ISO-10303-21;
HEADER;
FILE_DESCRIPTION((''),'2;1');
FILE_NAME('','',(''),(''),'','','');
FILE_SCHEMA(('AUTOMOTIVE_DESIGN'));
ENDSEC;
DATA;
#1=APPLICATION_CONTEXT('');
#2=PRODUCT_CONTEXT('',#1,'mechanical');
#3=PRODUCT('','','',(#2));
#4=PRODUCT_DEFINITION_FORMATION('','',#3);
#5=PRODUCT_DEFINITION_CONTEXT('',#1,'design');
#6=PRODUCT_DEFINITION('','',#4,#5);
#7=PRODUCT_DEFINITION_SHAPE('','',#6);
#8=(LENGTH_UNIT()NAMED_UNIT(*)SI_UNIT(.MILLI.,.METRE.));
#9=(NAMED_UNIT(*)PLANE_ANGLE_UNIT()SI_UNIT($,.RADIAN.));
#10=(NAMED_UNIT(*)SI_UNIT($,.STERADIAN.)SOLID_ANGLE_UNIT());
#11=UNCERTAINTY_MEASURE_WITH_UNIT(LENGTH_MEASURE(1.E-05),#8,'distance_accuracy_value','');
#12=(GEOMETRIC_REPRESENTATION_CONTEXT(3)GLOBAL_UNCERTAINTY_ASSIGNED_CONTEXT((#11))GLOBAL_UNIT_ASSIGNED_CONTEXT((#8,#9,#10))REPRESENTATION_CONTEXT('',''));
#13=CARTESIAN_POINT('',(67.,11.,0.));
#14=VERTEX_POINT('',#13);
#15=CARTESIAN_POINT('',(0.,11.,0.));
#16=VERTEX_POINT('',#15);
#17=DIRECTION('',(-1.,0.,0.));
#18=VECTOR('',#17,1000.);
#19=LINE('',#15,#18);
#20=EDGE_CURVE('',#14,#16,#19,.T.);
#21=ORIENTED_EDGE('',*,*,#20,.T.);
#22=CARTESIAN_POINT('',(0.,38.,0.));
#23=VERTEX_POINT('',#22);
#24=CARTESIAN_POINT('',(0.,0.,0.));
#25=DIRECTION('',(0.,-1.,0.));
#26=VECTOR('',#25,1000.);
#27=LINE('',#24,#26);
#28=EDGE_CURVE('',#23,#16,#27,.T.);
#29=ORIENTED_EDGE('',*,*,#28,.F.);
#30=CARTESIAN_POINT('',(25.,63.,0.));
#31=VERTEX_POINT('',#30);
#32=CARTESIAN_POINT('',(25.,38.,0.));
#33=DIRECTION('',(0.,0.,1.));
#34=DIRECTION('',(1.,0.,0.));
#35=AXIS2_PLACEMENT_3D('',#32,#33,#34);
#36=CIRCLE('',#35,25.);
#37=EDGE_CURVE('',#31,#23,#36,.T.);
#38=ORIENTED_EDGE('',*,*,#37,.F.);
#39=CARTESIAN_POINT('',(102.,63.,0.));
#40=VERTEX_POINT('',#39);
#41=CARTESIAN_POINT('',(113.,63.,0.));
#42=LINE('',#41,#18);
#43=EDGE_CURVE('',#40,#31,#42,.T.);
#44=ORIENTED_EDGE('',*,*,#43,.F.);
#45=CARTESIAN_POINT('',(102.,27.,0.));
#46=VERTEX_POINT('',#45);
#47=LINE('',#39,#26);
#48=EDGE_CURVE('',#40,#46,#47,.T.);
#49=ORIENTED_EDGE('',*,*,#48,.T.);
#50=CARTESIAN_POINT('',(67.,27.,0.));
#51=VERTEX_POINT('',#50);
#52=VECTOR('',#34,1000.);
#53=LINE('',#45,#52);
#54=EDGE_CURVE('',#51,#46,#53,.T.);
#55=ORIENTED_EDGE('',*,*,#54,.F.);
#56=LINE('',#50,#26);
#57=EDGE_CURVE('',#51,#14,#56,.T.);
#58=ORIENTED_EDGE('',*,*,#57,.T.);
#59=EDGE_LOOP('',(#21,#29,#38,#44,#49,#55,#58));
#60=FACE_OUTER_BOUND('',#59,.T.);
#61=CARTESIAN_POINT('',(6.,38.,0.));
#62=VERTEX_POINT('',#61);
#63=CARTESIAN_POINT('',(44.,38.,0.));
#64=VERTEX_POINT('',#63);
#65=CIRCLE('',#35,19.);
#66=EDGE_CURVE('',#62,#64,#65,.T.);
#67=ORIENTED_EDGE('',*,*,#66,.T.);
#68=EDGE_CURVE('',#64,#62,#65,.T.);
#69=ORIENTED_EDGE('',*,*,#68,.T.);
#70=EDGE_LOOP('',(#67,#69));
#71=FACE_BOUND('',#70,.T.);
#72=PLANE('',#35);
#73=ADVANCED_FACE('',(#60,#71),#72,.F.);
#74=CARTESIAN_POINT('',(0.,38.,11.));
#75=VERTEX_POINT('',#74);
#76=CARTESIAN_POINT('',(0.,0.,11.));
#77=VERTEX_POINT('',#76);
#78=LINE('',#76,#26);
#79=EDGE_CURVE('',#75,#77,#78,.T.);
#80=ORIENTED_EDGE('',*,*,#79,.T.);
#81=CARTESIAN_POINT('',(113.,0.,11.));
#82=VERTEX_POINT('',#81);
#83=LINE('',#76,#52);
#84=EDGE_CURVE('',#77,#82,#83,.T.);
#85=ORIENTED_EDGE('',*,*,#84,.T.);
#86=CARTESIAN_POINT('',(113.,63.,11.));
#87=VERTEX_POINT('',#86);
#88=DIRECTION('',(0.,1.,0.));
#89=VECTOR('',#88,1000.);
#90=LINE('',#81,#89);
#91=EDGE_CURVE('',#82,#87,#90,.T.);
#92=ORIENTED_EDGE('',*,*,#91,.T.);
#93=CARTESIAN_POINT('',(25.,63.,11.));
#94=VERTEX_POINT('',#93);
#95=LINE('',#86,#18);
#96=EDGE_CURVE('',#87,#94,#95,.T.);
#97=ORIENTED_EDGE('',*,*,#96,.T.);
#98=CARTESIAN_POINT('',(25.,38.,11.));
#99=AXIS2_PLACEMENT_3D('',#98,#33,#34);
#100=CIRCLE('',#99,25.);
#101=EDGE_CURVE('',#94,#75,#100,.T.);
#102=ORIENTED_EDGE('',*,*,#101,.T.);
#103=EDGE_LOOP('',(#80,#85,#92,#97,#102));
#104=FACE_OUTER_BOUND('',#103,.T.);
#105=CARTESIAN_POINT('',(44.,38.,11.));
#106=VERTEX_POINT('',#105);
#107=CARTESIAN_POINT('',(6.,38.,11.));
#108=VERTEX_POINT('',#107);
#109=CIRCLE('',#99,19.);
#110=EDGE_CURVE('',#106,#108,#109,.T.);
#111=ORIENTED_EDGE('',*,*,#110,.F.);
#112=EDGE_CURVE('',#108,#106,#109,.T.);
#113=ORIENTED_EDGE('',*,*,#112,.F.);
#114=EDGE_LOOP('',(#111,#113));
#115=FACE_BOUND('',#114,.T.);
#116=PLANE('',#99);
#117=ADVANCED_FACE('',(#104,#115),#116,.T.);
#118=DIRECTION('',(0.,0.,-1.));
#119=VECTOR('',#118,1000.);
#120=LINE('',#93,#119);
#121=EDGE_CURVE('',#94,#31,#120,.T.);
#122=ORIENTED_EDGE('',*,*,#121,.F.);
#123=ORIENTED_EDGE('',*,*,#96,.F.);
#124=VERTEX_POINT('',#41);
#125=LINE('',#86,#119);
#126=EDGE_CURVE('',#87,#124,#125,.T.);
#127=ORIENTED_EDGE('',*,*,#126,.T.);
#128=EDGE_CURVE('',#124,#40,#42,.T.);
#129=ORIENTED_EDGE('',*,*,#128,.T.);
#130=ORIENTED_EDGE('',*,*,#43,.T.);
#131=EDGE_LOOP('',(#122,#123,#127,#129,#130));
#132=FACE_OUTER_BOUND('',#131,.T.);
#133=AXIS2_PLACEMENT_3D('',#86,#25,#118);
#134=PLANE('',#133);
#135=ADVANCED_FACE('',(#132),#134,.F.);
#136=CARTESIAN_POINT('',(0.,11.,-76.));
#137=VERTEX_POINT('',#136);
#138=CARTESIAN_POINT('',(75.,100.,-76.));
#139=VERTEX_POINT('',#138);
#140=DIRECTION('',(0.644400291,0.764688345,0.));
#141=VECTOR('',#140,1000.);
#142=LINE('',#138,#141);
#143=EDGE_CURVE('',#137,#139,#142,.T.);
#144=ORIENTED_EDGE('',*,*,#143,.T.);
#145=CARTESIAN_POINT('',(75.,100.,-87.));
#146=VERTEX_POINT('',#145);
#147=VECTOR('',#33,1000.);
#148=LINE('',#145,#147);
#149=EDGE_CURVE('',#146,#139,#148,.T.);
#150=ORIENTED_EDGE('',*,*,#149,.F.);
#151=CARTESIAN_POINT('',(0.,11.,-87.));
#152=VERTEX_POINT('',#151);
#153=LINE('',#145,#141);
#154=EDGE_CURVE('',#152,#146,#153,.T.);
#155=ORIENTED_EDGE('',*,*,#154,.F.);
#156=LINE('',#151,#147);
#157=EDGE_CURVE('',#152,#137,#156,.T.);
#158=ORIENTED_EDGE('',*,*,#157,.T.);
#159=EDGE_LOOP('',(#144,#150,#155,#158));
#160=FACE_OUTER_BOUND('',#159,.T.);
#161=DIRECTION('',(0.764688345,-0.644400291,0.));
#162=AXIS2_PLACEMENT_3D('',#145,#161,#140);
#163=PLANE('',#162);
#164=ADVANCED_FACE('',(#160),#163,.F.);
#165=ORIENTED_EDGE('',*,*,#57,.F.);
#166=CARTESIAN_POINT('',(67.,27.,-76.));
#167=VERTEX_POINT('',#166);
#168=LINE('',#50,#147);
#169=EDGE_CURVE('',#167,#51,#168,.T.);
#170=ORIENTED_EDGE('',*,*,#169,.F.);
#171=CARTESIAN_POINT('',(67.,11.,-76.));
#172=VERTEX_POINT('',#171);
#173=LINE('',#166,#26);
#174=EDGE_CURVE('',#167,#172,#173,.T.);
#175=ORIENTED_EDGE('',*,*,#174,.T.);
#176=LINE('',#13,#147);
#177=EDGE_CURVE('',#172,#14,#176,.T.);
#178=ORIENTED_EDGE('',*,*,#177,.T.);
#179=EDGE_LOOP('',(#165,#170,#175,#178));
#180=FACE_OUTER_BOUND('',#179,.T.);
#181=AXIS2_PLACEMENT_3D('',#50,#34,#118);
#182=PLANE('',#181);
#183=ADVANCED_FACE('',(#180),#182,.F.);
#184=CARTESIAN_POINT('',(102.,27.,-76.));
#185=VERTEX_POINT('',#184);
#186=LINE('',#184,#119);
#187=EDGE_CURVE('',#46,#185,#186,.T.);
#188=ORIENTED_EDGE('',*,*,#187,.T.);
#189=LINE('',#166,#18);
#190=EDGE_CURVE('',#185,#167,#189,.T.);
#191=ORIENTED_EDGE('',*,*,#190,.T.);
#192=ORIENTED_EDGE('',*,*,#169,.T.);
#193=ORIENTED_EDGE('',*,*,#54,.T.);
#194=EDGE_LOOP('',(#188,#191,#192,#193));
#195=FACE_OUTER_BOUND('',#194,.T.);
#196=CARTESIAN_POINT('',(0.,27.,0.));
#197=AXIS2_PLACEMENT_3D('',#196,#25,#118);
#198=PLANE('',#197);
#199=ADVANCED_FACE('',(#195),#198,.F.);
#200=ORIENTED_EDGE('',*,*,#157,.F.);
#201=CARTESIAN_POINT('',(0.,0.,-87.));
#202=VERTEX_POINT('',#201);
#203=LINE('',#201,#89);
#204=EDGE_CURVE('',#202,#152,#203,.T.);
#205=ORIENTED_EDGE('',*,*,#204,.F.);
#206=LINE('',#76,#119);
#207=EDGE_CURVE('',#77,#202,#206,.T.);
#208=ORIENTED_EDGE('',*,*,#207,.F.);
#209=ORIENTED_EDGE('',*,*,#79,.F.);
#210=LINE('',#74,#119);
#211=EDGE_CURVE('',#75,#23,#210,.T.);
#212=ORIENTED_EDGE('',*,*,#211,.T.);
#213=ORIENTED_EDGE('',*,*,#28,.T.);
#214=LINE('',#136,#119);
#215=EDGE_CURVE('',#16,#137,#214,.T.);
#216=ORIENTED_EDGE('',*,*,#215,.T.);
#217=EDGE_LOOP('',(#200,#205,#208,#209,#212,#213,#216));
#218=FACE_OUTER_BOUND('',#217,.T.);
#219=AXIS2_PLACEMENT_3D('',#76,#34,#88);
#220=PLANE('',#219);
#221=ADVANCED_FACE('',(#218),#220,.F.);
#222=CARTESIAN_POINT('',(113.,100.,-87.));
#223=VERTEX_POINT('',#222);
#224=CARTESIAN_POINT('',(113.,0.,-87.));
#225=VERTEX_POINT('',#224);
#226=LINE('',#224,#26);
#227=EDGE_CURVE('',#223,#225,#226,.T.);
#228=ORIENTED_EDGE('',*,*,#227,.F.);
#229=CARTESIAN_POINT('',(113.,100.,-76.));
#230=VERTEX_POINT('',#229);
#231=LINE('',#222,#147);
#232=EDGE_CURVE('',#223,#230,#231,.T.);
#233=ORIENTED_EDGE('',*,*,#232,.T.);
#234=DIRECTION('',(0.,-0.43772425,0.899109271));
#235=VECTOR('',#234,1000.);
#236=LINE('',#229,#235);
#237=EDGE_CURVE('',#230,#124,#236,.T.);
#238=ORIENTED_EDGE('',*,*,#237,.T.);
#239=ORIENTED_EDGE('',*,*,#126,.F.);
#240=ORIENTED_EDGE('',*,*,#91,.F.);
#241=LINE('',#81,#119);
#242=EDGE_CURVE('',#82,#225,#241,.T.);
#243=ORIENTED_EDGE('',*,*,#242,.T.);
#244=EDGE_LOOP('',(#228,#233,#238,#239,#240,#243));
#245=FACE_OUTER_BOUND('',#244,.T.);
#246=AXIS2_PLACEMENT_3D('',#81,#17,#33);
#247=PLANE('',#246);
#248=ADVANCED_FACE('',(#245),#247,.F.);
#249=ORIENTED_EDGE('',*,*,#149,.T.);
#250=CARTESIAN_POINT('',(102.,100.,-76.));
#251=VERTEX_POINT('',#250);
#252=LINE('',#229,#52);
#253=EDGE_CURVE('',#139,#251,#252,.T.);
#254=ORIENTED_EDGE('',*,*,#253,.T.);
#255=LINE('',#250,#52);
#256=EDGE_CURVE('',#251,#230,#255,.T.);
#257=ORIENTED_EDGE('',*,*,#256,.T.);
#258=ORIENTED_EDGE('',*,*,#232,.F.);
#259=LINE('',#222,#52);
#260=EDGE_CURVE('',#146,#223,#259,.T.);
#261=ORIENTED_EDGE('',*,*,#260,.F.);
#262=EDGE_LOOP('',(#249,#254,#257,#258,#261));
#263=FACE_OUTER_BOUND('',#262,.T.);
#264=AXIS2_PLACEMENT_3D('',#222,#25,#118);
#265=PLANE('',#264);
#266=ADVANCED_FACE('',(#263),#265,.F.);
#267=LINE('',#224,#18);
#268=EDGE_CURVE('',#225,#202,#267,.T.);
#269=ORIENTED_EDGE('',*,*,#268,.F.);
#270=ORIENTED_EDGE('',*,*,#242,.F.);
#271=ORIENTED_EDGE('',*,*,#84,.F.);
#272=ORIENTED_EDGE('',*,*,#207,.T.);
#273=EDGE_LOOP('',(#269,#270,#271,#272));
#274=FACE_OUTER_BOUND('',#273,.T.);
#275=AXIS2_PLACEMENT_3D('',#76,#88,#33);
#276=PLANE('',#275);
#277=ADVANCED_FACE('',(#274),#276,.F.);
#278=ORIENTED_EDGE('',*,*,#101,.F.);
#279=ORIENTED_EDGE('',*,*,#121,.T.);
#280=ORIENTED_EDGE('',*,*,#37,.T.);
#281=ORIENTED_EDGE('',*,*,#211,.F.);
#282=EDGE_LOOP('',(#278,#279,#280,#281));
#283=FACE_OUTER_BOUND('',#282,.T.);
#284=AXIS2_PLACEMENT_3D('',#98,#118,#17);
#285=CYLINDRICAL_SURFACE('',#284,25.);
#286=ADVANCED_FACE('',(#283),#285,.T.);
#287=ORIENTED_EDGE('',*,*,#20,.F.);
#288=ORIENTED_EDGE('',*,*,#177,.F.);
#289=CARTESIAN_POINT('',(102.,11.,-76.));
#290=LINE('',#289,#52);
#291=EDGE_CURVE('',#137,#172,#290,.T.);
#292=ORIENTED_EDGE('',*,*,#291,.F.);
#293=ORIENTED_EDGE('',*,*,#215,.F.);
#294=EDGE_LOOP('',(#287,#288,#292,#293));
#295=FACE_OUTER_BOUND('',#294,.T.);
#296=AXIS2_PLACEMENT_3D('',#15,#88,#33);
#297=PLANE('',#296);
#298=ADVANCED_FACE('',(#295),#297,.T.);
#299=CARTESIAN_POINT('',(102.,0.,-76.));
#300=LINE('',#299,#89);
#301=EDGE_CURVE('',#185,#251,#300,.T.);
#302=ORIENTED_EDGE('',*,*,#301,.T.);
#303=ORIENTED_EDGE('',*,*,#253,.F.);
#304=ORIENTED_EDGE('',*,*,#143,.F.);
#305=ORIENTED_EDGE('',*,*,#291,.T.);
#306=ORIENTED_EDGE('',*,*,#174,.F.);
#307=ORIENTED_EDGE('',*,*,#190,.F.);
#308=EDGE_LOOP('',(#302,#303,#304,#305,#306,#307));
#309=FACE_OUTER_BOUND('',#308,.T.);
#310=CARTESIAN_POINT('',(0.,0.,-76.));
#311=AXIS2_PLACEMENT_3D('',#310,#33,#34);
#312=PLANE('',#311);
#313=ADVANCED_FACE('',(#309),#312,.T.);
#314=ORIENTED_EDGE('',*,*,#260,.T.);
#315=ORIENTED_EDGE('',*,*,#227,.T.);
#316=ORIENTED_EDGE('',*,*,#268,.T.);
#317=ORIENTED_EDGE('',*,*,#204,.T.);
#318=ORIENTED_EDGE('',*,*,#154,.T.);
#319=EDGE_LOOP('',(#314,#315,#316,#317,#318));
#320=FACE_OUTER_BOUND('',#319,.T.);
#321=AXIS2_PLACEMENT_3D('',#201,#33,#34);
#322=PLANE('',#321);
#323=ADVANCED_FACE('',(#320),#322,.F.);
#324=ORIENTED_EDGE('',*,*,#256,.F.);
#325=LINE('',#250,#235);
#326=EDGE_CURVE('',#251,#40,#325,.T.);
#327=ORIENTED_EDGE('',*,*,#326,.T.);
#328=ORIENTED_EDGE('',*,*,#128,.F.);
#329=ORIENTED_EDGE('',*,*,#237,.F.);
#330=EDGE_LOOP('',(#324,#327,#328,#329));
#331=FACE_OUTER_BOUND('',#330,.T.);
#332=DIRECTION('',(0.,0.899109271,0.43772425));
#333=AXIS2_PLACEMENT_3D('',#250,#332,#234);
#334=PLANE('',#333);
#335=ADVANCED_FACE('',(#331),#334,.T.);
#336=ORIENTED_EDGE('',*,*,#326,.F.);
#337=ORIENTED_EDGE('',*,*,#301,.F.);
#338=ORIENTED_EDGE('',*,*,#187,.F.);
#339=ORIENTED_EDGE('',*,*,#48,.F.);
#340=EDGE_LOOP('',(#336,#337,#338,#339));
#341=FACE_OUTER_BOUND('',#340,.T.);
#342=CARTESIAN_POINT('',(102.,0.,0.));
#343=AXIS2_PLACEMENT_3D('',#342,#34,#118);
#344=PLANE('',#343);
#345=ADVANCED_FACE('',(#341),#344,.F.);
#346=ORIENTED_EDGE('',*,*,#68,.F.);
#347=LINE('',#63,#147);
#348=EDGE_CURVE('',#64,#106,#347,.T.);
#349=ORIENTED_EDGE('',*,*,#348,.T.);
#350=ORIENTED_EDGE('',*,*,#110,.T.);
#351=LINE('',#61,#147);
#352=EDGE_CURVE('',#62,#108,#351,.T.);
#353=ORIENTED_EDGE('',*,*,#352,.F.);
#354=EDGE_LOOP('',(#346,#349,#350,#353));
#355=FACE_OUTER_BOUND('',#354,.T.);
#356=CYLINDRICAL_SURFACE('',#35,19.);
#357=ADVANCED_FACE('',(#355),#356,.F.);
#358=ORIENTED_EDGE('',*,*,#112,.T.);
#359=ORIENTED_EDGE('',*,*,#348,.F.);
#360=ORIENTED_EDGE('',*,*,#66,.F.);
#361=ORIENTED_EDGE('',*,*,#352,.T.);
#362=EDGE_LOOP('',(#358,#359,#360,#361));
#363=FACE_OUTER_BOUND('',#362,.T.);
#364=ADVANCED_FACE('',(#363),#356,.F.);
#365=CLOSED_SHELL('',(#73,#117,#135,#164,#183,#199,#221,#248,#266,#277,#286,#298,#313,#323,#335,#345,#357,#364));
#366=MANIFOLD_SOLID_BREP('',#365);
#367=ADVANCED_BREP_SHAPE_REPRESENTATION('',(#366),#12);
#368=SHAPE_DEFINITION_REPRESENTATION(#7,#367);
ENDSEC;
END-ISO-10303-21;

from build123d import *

# Parameters (mm, degrees)
EYE_PLATE_11MM_DEPTH    = 11
FLOOR_PLATE_11MM_DEPTH  = 11
SIDE_WALL_11MM_DEPTH    = 11
INCLINED_WEB_PROFILE_W  = 102
INCLINED_WEB_PROFILE_H  = 76
INCLINED_WEB_11MM_DEPTH = 11
END_CAP_PROFILE_W       = 35
END_CAP_PROFILE_H       = 76
END_CAP_16MM_DEPTH      = 16
PIVOT_BORE_PROFILE_R    = 19
PIVOT_BORE_38_DEPTH     = 11


with BuildPart() as part:
    # Eye Plate Profile → Eye Plate 11mm (new body)
    with BuildSketch(Plane.XY):
        with BuildLine():
            Line((0, 0), (113, 0))
            Line((113, 0), (113, 63))
            Line((113, 63), (25, 63))
            ThreePointArc((25, 63), (7.32233047, 55.67766953), (0, 38))
            Line((0, 38), (0, 0))
        make_face()
    extrude(amount=EYE_PLATE_11MM_DEPTH)

    # Floor Plate Profile → Floor Plate 11mm (add)
    with BuildSketch(Plane(origin=(113, 0, 0), x_dir=(0, 0, -1), z_dir=(1, 0, 0))):
        Polygon((0, 0), (76, 0), (76, 100), (0, 63), align=None)
    extrude(amount=-FLOOR_PLATE_11MM_DEPTH)

    # Side Wall Profile → Side Wall 11mm (add)
    with BuildSketch(Plane(origin=(0, 0, -76), x_dir=(-1, 0, 0), z_dir=(0, 0, -1))):
        Polygon((-113, 0), (0, 0), (0, 11), (-75, 100), (-113, 100), align=None)
    extrude(amount=SIDE_WALL_11MM_DEPTH)

    # Inclined Web Profile → Inclined Web 11mm (add)
    with BuildSketch(Plane.XZ):
        with Locations((51, -38)):
            Rectangle(INCLINED_WEB_PROFILE_W, INCLINED_WEB_PROFILE_H)
    extrude(amount=-INCLINED_WEB_11MM_DEPTH)

    # End Cap Profile → End Cap 16mm (add)
    with BuildSketch(Plane(origin=(0, 11, 0), x_dir=(1, 0, 0), z_dir=(0, 1, 0))):
        with Locations((84.5, 38)):
            Rectangle(END_CAP_PROFILE_W, END_CAP_PROFILE_H)
    extrude(amount=END_CAP_16MM_DEPTH)

    # Pivot Bore Profile → Pivot Bore Ø38 (cut)
    with BuildSketch(Plane.XY.offset(11)):
        with Locations((25, 38)):
            Circle(PIVOT_BORE_PROFILE_R)
    extrude(amount=-PIVOT_BORE_38_DEPTH, mode=Mode.SUBTRACT)


solid = part.part
